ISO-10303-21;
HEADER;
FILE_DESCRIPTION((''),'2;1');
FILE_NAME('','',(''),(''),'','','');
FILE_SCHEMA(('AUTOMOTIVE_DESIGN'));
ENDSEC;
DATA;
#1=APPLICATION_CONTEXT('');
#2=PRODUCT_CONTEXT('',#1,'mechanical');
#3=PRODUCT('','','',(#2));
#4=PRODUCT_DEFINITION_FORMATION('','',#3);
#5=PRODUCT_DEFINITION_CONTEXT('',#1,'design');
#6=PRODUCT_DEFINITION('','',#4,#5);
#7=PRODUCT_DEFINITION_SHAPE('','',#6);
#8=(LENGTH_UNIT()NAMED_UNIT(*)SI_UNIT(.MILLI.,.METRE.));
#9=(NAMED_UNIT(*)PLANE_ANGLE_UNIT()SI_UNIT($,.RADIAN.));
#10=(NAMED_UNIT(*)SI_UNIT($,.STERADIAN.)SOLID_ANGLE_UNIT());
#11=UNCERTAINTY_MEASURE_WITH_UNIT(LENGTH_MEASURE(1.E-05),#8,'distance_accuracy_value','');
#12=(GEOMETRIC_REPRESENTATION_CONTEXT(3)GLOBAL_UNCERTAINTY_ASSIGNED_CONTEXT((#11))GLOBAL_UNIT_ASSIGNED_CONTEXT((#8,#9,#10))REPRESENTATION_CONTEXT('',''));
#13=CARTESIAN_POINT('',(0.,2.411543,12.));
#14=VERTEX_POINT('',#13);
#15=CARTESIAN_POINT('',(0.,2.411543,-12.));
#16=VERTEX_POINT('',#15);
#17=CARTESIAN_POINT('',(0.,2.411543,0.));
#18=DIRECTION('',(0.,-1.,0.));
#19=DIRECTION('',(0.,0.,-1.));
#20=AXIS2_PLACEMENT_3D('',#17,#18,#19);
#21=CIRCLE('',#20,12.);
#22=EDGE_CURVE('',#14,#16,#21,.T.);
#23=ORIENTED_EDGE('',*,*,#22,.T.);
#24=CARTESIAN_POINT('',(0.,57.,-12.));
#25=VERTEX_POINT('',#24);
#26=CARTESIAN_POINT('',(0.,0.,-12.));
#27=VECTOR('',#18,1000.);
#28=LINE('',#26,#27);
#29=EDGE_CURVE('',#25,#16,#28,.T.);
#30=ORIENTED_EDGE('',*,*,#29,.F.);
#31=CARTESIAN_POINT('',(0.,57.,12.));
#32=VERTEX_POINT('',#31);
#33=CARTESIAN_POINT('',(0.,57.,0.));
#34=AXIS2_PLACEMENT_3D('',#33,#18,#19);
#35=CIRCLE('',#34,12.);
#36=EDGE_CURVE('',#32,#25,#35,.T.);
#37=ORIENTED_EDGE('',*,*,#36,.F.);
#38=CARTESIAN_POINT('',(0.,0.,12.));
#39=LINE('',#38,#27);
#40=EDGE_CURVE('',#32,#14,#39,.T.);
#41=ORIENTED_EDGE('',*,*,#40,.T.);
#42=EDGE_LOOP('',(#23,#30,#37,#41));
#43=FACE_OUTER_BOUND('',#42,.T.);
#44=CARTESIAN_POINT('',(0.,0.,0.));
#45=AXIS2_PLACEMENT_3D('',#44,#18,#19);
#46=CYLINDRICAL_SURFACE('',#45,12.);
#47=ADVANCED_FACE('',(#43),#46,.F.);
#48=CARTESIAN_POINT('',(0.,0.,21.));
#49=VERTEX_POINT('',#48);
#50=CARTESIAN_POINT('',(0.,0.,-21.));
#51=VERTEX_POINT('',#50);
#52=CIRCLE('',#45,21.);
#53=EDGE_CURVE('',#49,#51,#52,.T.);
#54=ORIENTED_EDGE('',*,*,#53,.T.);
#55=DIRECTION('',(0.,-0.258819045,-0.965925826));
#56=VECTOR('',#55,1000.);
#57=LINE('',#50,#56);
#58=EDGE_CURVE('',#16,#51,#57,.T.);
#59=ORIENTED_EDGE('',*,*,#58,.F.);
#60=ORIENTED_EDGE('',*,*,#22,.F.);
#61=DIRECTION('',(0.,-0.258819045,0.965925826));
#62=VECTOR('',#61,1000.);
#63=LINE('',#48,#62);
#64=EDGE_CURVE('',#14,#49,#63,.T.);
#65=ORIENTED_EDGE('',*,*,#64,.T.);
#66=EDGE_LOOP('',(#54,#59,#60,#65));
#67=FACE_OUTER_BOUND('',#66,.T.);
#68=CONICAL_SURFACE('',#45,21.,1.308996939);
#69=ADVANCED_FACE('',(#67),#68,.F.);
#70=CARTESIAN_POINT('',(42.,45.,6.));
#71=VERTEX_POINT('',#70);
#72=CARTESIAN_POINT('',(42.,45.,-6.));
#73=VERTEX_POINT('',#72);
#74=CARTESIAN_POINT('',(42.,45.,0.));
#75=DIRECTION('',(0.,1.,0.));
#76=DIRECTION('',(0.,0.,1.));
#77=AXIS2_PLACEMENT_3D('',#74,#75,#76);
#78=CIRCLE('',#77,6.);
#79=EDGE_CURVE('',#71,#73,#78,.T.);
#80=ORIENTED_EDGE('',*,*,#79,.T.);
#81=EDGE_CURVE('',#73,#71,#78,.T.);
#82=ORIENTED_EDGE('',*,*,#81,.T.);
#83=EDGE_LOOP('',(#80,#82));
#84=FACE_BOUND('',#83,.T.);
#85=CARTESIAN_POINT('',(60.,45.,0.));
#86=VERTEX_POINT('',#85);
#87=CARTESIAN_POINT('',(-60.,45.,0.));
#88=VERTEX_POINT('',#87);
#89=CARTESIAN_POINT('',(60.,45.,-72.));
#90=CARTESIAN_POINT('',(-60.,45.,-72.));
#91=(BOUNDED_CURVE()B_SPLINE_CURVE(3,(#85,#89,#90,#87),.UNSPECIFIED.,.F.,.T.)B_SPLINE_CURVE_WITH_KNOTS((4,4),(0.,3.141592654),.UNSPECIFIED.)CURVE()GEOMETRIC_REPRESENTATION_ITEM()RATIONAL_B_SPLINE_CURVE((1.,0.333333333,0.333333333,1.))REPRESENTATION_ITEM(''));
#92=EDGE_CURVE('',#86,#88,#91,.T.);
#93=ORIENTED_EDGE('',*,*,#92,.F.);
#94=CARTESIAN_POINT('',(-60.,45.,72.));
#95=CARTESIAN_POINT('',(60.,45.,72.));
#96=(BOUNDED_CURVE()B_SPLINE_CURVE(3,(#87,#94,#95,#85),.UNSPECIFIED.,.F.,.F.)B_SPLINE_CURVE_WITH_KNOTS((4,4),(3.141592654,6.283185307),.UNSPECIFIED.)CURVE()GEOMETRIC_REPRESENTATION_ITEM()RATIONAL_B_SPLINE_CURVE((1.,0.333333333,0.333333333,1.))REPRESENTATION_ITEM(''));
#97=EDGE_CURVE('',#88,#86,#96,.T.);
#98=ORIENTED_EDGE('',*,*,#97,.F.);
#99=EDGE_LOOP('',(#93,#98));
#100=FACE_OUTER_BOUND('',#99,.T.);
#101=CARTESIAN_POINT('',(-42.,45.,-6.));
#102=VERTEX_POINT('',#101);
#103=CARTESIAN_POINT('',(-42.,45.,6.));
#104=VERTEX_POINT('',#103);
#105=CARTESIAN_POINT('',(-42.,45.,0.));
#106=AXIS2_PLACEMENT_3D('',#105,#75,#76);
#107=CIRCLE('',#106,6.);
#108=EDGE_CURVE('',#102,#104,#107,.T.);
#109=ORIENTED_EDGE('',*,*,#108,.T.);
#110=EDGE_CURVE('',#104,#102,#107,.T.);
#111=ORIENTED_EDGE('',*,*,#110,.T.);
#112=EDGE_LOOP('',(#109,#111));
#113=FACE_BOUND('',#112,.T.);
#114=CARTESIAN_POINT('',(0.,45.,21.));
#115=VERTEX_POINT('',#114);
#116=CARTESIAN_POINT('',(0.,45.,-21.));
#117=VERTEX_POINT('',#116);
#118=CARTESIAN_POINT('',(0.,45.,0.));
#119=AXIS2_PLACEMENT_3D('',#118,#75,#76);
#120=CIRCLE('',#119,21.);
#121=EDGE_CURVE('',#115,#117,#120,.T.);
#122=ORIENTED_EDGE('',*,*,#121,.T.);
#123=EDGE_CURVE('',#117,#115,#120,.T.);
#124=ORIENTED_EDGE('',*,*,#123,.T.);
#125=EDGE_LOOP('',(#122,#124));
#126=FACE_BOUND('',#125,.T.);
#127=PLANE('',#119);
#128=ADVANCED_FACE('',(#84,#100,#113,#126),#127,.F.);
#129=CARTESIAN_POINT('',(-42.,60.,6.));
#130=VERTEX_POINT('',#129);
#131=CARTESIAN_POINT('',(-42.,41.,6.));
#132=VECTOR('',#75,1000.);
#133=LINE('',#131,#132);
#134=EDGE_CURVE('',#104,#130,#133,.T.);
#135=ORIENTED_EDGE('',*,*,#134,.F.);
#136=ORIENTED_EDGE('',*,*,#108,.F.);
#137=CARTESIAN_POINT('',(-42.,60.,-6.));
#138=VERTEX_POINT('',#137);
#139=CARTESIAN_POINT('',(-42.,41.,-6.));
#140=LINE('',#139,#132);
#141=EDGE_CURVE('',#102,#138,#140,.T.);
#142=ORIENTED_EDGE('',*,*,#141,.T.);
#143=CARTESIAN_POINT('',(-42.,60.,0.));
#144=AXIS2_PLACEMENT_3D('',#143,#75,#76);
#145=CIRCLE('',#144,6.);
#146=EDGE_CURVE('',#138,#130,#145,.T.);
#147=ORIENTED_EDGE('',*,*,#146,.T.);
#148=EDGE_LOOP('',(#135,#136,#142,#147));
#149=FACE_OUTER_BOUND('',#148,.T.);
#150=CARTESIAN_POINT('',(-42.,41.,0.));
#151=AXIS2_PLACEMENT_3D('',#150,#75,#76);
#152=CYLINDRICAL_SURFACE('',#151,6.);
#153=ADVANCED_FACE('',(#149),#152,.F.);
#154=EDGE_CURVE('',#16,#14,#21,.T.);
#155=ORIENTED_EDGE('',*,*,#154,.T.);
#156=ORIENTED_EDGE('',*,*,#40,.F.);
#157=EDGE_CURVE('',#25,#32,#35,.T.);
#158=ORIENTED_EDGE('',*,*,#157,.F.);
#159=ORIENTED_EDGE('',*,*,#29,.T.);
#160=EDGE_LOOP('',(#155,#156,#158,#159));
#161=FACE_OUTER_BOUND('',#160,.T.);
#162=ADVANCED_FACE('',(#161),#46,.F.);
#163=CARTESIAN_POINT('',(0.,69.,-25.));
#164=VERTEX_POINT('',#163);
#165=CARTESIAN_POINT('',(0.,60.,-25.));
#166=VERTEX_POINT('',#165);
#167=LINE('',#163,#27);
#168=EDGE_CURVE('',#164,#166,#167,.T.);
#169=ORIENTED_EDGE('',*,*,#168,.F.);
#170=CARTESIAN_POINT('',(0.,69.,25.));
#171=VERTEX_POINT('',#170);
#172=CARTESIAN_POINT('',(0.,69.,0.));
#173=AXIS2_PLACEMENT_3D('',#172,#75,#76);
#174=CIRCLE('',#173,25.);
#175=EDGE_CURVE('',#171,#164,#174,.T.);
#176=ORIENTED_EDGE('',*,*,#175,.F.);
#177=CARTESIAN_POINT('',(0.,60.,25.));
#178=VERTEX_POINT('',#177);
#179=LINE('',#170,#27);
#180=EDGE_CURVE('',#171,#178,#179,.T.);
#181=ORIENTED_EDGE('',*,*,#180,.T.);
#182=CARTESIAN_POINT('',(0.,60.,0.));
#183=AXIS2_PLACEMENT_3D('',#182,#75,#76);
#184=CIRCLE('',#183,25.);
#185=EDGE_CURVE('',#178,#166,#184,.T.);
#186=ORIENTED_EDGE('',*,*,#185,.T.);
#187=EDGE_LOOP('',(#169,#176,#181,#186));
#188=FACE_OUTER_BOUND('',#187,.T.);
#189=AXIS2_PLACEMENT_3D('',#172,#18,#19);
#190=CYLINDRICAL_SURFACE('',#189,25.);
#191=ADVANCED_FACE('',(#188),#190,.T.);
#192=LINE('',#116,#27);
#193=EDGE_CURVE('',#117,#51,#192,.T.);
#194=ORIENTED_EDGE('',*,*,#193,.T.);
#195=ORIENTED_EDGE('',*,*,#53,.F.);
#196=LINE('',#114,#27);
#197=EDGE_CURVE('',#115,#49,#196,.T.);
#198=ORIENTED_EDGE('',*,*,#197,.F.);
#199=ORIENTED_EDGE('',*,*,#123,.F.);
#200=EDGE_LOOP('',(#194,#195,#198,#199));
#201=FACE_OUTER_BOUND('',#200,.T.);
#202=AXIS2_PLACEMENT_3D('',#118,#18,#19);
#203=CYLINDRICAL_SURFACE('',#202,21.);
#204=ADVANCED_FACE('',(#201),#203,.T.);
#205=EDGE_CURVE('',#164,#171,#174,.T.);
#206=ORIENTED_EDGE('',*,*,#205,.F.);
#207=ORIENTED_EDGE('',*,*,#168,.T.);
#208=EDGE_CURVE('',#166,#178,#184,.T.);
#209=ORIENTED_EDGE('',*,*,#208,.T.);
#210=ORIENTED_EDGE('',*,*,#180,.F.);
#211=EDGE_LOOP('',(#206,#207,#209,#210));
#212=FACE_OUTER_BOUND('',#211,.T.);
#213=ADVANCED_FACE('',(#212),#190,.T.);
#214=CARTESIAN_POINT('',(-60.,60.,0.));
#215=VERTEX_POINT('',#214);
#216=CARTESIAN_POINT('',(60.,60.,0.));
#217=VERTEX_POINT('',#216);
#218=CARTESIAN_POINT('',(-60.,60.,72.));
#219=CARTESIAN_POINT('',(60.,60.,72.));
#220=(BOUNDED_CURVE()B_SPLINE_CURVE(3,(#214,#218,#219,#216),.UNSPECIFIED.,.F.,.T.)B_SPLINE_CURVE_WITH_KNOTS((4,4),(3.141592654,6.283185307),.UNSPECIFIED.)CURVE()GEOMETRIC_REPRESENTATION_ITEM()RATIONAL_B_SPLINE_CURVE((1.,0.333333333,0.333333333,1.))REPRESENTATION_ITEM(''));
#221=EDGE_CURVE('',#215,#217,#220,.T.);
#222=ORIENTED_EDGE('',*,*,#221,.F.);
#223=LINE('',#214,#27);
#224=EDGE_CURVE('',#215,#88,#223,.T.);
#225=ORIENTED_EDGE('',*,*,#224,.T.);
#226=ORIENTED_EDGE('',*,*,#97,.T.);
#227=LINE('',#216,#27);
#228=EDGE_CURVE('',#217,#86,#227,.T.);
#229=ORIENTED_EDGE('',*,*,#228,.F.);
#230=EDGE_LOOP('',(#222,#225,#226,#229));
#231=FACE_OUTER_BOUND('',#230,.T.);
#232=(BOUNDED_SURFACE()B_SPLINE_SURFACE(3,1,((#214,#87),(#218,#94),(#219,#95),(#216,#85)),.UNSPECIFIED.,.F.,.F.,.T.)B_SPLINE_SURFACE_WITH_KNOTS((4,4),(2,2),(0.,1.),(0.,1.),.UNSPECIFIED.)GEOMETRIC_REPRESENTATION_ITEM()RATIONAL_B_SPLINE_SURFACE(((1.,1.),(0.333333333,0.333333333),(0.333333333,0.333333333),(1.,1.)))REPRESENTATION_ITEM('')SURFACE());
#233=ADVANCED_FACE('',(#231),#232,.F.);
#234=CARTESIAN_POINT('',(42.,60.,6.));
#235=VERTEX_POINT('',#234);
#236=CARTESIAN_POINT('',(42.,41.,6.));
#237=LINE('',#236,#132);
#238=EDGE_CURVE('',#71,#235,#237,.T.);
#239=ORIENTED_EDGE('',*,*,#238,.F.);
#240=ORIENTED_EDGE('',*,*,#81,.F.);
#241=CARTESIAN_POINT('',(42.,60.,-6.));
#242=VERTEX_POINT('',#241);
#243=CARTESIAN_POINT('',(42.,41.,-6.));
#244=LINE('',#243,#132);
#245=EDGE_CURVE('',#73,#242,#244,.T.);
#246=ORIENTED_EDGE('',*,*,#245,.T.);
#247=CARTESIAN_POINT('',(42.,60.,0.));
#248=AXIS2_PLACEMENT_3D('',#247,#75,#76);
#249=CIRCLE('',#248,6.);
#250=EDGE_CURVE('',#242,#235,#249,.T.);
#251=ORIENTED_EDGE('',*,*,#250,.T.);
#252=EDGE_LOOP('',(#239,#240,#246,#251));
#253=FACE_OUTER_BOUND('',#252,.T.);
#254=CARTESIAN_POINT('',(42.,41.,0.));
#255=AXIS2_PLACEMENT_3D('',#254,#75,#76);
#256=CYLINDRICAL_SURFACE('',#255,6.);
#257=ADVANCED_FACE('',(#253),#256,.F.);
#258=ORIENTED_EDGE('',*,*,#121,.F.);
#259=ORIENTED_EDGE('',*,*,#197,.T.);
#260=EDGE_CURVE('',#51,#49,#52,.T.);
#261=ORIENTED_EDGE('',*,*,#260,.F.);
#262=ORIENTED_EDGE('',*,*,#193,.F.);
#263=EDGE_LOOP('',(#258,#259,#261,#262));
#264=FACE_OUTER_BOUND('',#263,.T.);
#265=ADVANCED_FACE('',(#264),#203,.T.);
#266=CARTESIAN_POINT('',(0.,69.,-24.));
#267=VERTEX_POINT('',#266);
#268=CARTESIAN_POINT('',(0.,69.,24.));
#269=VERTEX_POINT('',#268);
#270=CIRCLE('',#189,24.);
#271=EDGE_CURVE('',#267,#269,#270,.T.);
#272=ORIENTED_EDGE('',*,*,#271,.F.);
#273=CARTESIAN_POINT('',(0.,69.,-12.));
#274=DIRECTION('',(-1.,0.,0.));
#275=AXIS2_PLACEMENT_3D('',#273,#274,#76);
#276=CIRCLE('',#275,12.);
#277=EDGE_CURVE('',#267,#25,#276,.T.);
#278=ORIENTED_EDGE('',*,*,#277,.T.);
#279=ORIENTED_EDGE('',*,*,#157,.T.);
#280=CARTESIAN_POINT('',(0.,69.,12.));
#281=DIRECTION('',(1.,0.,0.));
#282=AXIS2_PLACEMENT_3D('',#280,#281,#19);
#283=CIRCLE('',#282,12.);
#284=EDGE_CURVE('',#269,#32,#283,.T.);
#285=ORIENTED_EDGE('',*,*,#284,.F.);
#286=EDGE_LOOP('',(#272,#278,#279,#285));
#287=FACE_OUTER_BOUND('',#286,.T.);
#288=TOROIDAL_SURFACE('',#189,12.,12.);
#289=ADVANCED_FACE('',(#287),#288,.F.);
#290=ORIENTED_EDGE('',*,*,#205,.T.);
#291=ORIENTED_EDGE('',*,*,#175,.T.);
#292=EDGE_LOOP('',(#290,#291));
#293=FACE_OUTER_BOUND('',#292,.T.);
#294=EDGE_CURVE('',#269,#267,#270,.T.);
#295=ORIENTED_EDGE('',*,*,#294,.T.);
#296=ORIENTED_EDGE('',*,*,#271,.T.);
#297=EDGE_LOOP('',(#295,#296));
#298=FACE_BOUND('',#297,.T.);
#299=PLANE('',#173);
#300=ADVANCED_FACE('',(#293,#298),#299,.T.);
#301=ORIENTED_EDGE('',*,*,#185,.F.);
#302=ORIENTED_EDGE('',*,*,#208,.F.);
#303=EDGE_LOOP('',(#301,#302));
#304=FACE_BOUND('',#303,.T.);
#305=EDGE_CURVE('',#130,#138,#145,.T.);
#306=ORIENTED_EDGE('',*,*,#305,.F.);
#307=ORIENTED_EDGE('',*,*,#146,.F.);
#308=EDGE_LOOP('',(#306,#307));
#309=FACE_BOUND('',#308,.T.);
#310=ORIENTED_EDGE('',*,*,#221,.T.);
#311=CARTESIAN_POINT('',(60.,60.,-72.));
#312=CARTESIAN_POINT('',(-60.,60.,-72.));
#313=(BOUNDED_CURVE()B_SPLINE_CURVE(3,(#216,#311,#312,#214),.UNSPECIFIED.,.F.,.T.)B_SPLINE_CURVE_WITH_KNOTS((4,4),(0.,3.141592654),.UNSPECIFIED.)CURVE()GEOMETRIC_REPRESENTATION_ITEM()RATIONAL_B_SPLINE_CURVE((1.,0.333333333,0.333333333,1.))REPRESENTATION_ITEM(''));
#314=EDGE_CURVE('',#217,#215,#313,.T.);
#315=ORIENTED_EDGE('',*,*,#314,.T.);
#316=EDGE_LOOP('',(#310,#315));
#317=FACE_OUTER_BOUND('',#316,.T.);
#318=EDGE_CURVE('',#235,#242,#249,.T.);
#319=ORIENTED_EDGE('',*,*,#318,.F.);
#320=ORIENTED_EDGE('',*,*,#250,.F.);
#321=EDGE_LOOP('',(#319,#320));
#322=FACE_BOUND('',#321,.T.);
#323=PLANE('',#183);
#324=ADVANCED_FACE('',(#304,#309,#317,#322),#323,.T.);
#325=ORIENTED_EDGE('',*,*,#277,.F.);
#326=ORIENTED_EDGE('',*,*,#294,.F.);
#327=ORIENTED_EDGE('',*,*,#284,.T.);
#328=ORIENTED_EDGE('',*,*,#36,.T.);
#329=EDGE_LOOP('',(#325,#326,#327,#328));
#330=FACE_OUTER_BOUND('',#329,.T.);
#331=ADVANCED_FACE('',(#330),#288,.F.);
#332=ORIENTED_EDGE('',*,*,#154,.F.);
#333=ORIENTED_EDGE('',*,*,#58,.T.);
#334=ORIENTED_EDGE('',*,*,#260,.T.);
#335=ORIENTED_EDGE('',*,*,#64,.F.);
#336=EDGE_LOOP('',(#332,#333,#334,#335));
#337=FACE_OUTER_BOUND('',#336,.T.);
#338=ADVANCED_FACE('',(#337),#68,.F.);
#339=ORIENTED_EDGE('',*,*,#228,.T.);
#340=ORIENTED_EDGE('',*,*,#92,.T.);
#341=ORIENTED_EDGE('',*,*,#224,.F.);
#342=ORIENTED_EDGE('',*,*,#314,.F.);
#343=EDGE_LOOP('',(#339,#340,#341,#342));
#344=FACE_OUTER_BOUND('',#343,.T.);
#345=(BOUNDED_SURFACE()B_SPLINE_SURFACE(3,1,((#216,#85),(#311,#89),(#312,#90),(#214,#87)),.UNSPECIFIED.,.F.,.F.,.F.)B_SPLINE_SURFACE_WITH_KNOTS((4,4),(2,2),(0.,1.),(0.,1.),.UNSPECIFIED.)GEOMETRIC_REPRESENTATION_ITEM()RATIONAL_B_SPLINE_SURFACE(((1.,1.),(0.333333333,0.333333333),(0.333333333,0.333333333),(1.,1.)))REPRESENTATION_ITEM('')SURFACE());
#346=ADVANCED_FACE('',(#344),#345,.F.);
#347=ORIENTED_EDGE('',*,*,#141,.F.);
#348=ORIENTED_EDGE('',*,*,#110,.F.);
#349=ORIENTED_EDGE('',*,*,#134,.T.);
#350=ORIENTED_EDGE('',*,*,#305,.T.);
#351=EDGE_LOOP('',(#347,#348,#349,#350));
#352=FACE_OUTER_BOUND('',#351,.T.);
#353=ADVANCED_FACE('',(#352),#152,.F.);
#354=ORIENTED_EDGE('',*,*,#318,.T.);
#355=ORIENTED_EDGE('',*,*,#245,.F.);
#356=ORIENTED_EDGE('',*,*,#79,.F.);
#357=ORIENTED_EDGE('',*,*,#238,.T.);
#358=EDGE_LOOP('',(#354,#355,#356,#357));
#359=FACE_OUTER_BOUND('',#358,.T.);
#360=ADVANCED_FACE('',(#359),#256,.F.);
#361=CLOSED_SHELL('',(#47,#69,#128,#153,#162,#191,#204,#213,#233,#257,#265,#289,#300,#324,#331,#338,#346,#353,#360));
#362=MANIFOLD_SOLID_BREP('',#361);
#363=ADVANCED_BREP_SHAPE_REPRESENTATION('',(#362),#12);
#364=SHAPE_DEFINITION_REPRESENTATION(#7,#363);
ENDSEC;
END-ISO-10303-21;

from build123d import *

# Parameters (mm, degrees)
SHANK_SKETCH_42_R          = 21
SHANK_42_DEPTH             = 45
FLANGE_SKETCH_120X36_RX    = 60
FLANGE_SKETCH_120X36_RY    = 36
OVAL_FLANGE_120X36_DEPTH   = 15
SPIGOT_SKETCH_50_R         = 25
SPIGOT_50_DEPTH            = 9
MOUNTING_HOLES_SKETCH_R    = 6
MOUNTING_HOLES_2X_12_DEPTH = 19


with BuildPart() as part:
    # Shank Sketch Ø42 → Shank Ø42 (new body)
    with BuildSketch(Plane(origin=(0, 0, 0), x_dir=(1, 0, 0), z_dir=(0, 1, 0))):
        with Locations(Location((0, 0, 0), (0, 0, 90))):
            Circle(SHANK_SKETCH_42_R)
    extrude(amount=SHANK_42_DEPTH)

    # Flange Sketch 120x36 → Oval Flange 120x36 (add)
    with BuildSketch(Plane(origin=(0, 45, 0), x_dir=(1, 0, 0), z_dir=(0, 1, 0))):
        with Locations((0, 0)):
            Ellipse(FLANGE_SKETCH_120X36_RX, FLANGE_SKETCH_120X36_RY)
    extrude(amount=OVAL_FLANGE_120X36_DEPTH)

    # Spigot Sketch Ø50 → Spigot Ø50 (add)
    with BuildSketch(Plane(origin=(0, 60, 0), x_dir=(1, 0, 0), z_dir=(0, 1, 0))):
        with Locations(Location((0, 0, 0), (0, 0, 270))):
            Circle(SPIGOT_SKETCH_50_R)
    extrude(amount=SPIGOT_50_DEPTH)

    # Bore Profile Sketch → Bore and Seat Cut (revolve, cut)
    with BuildSketch(Plane.XY, mode=Mode.PRIVATE) as bore_and_seat_cut_sk:
        with BuildLine():
            Line((21, 0), (12, 2.411542732))
            Line((12, 2.411542732), (12, 57))
            ThreePointArc((12, 57), (20.485281374, 60.514718626), (24, 69))
            Line((24, 69), (0, 69))
            Line((0, 69), (0, 0))
            Line((0, 0), (21, 0))
        make_face()
    revolve(bore_and_seat_cut_sk.sketch.rotate(Axis((0, 0, 0), (0, 1, 0)), 90), axis=Axis((0, 0, 0), (0, 1, 0)), mode=Mode.SUBTRACT)

    # Mounting Holes Sketch → Mounting Holes 2xØ12 (cut)
    with BuildSketch(Plane(origin=(0, 60, 0), x_dir=(1, 0, 0), z_dir=(0, 1, 0))):
        with Locations(Location((-42, 0, 0), (0, 0, 270))):
            Circle(MOUNTING_HOLES_SKETCH_R)
        with Locations(Location((42, 0, 0), (0, 0, 270))):
            Circle(MOUNTING_HOLES_SKETCH_R)
    extrude(amount=-MOUNTING_HOLES_2X_12_DEPTH, mode=Mode.SUBTRACT)


solid = part.part
